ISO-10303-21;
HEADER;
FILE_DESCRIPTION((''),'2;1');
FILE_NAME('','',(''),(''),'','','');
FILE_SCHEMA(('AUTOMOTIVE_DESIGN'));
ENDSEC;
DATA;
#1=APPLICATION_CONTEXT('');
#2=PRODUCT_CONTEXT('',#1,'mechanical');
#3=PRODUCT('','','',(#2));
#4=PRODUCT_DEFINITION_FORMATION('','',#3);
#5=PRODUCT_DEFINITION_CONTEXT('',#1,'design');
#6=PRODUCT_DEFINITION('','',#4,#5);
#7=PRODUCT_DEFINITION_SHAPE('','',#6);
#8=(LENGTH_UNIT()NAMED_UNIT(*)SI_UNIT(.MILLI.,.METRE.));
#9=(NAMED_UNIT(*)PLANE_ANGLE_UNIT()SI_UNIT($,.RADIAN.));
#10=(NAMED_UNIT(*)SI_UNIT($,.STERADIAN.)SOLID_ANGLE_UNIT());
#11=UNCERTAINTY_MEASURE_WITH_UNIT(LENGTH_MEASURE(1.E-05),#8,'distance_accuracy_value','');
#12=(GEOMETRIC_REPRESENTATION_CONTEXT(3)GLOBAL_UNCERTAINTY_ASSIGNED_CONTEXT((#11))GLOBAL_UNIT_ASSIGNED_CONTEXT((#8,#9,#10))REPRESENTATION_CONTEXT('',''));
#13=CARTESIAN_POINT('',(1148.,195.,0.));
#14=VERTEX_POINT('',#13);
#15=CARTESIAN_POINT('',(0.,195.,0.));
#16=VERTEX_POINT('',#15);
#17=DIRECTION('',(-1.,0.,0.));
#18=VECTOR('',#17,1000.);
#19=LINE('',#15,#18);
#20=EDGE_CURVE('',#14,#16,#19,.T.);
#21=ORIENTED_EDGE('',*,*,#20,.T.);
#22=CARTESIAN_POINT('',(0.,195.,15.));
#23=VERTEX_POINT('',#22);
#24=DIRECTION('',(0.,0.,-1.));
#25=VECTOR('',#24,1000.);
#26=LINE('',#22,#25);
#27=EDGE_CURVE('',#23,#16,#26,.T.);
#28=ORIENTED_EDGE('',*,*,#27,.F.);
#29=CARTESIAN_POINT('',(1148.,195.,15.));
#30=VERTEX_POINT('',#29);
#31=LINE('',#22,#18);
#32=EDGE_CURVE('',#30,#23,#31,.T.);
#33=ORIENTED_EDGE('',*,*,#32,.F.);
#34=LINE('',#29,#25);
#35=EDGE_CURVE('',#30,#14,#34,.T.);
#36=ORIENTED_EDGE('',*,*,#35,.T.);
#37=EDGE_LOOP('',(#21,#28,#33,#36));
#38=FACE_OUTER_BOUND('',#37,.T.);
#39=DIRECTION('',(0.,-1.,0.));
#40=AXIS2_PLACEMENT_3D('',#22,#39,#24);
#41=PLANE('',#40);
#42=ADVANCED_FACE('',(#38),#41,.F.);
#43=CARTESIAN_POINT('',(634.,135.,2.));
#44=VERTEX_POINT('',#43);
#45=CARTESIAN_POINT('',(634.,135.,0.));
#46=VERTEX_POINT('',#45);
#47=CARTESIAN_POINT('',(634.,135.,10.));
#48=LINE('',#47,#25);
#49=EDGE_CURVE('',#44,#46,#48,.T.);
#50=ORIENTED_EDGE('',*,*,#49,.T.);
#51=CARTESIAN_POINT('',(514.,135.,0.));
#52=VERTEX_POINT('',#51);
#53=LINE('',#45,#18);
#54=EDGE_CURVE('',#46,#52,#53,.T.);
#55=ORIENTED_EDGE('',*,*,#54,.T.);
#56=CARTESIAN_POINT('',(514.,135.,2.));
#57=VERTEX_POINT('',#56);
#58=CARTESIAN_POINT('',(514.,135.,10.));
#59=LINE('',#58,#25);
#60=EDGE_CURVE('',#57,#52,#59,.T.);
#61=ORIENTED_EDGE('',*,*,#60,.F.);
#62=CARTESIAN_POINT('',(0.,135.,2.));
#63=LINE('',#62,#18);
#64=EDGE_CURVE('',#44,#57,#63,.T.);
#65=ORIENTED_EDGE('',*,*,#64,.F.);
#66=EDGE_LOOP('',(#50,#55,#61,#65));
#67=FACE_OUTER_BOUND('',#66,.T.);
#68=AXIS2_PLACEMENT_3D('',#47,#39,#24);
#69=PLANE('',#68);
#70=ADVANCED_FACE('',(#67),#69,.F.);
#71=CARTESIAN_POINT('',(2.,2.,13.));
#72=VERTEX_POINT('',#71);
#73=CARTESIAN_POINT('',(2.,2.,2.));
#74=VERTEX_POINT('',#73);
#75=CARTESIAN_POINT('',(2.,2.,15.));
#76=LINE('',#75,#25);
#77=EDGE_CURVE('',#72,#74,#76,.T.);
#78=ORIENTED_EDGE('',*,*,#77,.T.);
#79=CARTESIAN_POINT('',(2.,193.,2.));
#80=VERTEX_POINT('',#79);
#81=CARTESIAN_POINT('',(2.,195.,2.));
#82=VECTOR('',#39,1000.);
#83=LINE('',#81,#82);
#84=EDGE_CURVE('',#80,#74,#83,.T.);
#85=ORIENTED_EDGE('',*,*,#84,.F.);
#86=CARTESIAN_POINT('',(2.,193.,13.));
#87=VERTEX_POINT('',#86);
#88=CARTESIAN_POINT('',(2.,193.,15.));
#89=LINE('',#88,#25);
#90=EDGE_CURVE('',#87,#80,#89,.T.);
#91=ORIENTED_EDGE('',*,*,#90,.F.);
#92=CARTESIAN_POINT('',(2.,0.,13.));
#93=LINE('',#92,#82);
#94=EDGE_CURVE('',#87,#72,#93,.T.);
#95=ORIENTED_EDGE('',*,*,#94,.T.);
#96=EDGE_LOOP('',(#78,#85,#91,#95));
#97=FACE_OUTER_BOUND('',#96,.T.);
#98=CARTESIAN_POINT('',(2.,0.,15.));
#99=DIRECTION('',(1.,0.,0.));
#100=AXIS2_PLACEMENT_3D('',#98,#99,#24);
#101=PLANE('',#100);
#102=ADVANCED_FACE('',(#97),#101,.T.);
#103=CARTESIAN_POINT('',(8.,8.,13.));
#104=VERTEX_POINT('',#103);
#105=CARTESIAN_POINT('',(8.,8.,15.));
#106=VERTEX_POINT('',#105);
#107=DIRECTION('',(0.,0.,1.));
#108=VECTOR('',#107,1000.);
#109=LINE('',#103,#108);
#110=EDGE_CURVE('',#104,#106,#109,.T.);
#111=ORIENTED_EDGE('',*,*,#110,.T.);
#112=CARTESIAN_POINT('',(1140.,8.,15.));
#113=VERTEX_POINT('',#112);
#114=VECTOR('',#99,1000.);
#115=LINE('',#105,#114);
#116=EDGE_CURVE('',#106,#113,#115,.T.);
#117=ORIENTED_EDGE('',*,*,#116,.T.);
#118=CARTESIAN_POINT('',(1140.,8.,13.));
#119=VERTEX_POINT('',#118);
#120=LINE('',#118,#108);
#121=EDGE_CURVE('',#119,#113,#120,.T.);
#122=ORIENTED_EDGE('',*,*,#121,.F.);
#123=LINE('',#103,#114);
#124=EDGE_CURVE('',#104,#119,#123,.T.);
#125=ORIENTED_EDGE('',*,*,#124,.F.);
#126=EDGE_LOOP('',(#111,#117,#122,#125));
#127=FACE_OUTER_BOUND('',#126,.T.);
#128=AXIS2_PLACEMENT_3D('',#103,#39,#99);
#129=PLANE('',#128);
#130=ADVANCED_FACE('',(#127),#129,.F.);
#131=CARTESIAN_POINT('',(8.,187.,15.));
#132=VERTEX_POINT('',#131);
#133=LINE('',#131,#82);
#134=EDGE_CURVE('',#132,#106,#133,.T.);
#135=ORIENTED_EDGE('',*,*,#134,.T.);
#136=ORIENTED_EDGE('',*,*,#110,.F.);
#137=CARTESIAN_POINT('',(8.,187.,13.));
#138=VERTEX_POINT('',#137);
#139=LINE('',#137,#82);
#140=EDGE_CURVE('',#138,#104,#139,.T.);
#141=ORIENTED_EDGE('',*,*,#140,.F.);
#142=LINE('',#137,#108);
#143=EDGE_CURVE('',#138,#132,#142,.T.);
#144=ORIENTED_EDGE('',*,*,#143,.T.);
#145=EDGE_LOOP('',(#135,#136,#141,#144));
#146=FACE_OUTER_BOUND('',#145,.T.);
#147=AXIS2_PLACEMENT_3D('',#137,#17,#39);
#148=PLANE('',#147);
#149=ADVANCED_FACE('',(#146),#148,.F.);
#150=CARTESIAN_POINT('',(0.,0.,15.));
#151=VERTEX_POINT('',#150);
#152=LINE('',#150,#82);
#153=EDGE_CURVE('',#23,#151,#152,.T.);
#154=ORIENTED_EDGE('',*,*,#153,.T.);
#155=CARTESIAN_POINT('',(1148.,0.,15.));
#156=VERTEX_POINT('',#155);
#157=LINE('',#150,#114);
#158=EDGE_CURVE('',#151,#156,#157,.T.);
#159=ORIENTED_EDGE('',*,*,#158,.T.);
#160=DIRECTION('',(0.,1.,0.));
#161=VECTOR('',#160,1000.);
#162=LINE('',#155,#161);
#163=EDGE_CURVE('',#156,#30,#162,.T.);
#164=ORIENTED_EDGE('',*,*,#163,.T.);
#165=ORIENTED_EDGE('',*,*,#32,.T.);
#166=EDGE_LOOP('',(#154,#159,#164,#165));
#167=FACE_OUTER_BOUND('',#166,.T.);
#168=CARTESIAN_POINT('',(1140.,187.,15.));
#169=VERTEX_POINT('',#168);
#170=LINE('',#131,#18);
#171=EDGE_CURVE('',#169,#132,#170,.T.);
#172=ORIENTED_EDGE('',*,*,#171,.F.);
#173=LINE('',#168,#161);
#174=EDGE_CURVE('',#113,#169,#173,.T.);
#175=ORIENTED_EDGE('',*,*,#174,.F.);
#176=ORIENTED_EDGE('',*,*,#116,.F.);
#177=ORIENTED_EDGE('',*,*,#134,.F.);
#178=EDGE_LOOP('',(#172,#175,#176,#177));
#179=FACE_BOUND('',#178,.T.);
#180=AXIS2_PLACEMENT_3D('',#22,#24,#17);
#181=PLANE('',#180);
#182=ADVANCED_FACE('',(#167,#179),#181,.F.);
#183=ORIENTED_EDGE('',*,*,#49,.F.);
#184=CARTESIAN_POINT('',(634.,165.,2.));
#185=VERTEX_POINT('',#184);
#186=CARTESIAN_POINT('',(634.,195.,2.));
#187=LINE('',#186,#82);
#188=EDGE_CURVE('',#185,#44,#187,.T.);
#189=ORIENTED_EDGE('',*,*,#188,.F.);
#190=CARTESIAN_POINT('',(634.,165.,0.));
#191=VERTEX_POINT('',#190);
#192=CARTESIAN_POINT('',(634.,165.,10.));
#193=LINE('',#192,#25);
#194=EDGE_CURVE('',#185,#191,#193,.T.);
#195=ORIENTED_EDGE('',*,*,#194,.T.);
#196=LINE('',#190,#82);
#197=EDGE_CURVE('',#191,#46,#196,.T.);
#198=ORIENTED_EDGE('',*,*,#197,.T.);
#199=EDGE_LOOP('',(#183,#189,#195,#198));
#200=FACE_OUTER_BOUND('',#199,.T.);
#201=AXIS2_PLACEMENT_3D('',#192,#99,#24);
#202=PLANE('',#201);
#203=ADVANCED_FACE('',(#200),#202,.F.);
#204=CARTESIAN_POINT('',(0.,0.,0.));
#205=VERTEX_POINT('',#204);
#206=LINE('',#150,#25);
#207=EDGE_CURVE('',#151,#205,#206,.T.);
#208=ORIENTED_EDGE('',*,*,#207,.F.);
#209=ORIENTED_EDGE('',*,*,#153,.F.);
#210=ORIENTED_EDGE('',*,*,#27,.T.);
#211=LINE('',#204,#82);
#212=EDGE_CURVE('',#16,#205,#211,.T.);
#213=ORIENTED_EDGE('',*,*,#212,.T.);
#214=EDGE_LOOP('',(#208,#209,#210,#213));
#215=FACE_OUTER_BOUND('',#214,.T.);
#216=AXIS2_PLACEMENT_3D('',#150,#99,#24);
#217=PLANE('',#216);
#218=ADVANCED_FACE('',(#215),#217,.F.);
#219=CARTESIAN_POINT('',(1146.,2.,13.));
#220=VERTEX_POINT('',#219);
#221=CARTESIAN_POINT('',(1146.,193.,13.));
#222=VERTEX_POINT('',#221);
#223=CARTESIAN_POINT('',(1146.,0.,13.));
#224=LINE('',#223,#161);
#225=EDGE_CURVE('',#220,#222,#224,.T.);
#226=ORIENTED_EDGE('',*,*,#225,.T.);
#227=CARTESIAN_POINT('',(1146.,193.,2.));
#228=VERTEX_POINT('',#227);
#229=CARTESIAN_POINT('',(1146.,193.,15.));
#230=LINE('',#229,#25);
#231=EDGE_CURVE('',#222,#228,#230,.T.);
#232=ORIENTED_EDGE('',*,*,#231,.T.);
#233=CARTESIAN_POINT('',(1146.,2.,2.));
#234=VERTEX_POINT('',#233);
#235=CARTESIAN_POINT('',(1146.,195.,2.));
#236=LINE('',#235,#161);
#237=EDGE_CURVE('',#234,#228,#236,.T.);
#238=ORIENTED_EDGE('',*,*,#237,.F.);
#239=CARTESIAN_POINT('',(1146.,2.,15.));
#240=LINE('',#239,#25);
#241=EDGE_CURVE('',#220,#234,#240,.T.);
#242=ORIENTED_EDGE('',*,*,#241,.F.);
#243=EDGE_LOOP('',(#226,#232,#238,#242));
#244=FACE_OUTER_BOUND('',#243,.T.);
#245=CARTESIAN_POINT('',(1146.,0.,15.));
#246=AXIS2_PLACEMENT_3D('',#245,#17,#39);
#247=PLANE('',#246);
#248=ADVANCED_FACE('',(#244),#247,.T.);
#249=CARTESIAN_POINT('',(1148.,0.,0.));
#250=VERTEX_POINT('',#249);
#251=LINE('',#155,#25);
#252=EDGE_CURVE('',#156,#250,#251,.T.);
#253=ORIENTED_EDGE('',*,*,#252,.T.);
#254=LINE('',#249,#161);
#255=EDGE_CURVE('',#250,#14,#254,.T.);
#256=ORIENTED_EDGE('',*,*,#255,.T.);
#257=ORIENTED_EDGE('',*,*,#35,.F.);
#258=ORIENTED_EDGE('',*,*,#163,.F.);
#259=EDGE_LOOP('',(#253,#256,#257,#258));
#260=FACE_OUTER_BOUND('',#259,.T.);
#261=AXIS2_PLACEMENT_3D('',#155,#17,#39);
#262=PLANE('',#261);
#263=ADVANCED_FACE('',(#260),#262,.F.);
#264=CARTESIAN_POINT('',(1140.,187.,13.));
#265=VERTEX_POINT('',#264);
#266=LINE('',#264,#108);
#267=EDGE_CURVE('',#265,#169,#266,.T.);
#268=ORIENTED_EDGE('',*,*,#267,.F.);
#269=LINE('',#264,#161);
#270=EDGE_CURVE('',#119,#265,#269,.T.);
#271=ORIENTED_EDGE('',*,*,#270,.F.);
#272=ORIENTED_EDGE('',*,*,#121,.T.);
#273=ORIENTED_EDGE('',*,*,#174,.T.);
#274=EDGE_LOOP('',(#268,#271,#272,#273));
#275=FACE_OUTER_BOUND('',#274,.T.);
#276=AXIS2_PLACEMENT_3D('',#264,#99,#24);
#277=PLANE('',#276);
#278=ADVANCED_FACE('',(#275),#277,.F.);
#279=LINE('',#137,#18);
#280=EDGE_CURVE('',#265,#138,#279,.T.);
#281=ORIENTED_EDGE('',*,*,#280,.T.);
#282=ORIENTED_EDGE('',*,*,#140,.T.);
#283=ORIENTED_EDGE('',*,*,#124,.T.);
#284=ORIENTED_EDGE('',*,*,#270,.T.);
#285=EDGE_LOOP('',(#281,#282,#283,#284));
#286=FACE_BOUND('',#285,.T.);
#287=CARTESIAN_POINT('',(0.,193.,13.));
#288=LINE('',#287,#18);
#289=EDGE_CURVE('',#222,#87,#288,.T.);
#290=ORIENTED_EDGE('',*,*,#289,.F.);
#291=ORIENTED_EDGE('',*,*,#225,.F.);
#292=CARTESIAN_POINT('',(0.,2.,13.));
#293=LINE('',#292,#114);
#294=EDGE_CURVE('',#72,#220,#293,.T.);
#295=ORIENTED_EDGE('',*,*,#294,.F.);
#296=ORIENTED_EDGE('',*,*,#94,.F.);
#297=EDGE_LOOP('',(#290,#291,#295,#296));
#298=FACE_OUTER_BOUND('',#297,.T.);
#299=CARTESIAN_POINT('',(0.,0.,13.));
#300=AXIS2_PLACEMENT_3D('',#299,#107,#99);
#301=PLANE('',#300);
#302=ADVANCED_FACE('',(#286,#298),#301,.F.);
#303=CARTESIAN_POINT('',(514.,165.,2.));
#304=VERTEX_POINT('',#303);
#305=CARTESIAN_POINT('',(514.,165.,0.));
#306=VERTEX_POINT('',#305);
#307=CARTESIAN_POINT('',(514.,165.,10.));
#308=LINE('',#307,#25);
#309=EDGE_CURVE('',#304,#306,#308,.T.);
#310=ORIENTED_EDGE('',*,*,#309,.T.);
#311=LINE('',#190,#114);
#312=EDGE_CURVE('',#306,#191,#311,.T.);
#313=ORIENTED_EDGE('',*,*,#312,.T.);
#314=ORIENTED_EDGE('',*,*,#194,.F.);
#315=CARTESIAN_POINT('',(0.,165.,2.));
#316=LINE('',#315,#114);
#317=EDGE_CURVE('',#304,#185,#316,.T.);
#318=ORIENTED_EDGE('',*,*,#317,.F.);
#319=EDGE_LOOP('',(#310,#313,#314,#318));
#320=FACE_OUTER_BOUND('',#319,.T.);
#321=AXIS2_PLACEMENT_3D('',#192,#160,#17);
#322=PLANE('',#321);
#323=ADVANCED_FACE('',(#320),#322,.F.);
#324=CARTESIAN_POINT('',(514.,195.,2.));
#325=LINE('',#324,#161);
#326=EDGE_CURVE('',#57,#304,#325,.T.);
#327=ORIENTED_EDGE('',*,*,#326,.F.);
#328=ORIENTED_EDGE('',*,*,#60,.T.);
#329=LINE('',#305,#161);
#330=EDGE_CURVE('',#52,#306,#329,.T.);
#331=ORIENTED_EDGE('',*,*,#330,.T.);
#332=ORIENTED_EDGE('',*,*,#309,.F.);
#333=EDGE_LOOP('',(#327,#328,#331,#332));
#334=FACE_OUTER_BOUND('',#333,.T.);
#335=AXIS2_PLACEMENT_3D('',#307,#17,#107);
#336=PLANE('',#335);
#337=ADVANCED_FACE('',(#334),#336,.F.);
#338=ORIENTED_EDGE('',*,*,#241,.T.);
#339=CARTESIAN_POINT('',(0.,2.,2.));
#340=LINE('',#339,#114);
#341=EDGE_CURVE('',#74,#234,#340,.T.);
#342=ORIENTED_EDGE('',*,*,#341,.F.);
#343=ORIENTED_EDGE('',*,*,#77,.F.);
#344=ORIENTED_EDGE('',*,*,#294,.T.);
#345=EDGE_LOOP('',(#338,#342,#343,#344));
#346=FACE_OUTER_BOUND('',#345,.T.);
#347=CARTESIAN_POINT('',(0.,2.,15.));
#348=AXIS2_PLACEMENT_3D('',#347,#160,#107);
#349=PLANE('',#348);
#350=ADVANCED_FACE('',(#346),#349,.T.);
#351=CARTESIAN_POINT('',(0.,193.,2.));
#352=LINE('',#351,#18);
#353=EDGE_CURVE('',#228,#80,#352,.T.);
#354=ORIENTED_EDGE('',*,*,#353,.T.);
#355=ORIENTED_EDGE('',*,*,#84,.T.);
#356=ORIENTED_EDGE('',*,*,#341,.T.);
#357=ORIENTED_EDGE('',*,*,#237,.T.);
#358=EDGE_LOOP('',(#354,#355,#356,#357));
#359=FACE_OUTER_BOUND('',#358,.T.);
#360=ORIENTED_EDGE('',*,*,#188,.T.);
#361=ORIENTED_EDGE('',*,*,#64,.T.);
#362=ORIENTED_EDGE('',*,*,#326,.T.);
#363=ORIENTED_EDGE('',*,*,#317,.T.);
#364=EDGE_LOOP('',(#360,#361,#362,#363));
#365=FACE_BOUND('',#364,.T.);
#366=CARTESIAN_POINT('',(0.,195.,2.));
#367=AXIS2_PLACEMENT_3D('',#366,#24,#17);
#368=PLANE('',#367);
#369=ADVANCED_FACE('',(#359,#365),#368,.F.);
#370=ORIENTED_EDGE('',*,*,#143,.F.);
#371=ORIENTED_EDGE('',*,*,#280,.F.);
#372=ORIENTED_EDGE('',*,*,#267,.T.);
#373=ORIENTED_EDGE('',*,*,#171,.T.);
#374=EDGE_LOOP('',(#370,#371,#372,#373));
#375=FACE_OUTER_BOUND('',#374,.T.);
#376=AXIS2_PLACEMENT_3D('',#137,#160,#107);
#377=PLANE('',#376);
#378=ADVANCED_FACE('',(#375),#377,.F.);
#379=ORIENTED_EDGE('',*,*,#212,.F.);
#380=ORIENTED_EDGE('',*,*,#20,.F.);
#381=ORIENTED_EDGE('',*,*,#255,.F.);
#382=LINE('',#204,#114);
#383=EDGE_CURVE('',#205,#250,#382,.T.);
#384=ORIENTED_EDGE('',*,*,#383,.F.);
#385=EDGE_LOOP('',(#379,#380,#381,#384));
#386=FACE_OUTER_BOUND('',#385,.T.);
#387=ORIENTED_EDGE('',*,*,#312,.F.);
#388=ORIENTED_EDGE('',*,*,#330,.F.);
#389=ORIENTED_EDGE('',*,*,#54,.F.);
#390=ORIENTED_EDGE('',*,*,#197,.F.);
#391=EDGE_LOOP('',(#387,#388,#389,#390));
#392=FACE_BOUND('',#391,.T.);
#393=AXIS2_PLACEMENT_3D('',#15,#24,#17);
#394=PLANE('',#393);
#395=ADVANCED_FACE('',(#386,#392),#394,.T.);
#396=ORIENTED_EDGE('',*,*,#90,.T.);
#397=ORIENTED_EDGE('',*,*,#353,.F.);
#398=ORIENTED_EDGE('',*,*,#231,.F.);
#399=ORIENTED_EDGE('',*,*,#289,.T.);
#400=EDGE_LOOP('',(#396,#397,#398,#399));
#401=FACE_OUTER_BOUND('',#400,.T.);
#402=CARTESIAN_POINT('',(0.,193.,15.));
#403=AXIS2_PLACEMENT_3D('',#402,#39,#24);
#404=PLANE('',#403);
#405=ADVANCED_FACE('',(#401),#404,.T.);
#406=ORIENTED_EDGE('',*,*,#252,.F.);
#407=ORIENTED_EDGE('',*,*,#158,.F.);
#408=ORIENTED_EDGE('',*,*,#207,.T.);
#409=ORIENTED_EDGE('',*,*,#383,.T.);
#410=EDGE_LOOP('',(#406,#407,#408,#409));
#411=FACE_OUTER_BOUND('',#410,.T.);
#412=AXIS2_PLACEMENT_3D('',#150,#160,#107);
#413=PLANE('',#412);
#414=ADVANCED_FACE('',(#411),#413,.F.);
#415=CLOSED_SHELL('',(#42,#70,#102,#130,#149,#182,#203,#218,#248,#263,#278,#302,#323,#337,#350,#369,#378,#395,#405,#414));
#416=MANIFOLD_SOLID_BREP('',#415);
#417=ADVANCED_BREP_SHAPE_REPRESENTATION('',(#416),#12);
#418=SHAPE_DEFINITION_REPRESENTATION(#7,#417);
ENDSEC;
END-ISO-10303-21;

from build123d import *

# Parameters (mm, degrees)
SKETCH_1_W          = 1148
SKETCH_1_H          = 195
EXTRUDE_1_DEPTH     = 15
SHELL_1_T           = -2
SKETCH_2_W          = 1148
SKETCH_2_H          = 195
SKETCH_2_W_2        = 1132
SKETCH_2_H_2        = 179
EXTRUDE_2_DEPTH     = 2
SKETCH_3_W          = 120
SKETCH_3_H          = 30
CUT_EXTRUDE_1_DEPTH = 10


with BuildPart() as part:
    # 草图1 → 凸台-拉伸1 (new body)
    with BuildSketch(Plane.XY):
        with Locations((574, 97.5)):
            Rectangle(SKETCH_1_W, SKETCH_1_H)
    extrude(amount=EXTRUDE_1_DEPTH)

    # 抽壳1
    shell_1_openings = [part.faces().sort_by_distance(p)[0] for p in [
        (574, 97.5, 15),
    ]]
    offset(amount=SHELL_1_T, openings=shell_1_openings, kind=Kind.INTERSECTION)

    # 草图2 → 凸台-拉伸2 (add)
    with BuildSketch(Plane.XY.offset(15)):
        with Locations((574, 97.5)):
            Rectangle(SKETCH_2_W, SKETCH_2_H)
        with Locations((574, 97.5)):
            Rectangle(SKETCH_2_W_2, SKETCH_2_H_2, mode=Mode.SUBTRACT)
    extrude(amount=-EXTRUDE_2_DEPTH)

    # 草图3 → 切除-拉伸1 (cut)
    with BuildSketch(Plane(origin=(0, 0, 0), x_dir=(-1, 0, 0), z_dir=(0, 0, -1))):
        with Locations((-574, 150)):
            Rectangle(SKETCH_3_W, SKETCH_3_H)
    extrude(amount=-CUT_EXTRUDE_1_DEPTH, mode=Mode.SUBTRACT)


solid = part.part
